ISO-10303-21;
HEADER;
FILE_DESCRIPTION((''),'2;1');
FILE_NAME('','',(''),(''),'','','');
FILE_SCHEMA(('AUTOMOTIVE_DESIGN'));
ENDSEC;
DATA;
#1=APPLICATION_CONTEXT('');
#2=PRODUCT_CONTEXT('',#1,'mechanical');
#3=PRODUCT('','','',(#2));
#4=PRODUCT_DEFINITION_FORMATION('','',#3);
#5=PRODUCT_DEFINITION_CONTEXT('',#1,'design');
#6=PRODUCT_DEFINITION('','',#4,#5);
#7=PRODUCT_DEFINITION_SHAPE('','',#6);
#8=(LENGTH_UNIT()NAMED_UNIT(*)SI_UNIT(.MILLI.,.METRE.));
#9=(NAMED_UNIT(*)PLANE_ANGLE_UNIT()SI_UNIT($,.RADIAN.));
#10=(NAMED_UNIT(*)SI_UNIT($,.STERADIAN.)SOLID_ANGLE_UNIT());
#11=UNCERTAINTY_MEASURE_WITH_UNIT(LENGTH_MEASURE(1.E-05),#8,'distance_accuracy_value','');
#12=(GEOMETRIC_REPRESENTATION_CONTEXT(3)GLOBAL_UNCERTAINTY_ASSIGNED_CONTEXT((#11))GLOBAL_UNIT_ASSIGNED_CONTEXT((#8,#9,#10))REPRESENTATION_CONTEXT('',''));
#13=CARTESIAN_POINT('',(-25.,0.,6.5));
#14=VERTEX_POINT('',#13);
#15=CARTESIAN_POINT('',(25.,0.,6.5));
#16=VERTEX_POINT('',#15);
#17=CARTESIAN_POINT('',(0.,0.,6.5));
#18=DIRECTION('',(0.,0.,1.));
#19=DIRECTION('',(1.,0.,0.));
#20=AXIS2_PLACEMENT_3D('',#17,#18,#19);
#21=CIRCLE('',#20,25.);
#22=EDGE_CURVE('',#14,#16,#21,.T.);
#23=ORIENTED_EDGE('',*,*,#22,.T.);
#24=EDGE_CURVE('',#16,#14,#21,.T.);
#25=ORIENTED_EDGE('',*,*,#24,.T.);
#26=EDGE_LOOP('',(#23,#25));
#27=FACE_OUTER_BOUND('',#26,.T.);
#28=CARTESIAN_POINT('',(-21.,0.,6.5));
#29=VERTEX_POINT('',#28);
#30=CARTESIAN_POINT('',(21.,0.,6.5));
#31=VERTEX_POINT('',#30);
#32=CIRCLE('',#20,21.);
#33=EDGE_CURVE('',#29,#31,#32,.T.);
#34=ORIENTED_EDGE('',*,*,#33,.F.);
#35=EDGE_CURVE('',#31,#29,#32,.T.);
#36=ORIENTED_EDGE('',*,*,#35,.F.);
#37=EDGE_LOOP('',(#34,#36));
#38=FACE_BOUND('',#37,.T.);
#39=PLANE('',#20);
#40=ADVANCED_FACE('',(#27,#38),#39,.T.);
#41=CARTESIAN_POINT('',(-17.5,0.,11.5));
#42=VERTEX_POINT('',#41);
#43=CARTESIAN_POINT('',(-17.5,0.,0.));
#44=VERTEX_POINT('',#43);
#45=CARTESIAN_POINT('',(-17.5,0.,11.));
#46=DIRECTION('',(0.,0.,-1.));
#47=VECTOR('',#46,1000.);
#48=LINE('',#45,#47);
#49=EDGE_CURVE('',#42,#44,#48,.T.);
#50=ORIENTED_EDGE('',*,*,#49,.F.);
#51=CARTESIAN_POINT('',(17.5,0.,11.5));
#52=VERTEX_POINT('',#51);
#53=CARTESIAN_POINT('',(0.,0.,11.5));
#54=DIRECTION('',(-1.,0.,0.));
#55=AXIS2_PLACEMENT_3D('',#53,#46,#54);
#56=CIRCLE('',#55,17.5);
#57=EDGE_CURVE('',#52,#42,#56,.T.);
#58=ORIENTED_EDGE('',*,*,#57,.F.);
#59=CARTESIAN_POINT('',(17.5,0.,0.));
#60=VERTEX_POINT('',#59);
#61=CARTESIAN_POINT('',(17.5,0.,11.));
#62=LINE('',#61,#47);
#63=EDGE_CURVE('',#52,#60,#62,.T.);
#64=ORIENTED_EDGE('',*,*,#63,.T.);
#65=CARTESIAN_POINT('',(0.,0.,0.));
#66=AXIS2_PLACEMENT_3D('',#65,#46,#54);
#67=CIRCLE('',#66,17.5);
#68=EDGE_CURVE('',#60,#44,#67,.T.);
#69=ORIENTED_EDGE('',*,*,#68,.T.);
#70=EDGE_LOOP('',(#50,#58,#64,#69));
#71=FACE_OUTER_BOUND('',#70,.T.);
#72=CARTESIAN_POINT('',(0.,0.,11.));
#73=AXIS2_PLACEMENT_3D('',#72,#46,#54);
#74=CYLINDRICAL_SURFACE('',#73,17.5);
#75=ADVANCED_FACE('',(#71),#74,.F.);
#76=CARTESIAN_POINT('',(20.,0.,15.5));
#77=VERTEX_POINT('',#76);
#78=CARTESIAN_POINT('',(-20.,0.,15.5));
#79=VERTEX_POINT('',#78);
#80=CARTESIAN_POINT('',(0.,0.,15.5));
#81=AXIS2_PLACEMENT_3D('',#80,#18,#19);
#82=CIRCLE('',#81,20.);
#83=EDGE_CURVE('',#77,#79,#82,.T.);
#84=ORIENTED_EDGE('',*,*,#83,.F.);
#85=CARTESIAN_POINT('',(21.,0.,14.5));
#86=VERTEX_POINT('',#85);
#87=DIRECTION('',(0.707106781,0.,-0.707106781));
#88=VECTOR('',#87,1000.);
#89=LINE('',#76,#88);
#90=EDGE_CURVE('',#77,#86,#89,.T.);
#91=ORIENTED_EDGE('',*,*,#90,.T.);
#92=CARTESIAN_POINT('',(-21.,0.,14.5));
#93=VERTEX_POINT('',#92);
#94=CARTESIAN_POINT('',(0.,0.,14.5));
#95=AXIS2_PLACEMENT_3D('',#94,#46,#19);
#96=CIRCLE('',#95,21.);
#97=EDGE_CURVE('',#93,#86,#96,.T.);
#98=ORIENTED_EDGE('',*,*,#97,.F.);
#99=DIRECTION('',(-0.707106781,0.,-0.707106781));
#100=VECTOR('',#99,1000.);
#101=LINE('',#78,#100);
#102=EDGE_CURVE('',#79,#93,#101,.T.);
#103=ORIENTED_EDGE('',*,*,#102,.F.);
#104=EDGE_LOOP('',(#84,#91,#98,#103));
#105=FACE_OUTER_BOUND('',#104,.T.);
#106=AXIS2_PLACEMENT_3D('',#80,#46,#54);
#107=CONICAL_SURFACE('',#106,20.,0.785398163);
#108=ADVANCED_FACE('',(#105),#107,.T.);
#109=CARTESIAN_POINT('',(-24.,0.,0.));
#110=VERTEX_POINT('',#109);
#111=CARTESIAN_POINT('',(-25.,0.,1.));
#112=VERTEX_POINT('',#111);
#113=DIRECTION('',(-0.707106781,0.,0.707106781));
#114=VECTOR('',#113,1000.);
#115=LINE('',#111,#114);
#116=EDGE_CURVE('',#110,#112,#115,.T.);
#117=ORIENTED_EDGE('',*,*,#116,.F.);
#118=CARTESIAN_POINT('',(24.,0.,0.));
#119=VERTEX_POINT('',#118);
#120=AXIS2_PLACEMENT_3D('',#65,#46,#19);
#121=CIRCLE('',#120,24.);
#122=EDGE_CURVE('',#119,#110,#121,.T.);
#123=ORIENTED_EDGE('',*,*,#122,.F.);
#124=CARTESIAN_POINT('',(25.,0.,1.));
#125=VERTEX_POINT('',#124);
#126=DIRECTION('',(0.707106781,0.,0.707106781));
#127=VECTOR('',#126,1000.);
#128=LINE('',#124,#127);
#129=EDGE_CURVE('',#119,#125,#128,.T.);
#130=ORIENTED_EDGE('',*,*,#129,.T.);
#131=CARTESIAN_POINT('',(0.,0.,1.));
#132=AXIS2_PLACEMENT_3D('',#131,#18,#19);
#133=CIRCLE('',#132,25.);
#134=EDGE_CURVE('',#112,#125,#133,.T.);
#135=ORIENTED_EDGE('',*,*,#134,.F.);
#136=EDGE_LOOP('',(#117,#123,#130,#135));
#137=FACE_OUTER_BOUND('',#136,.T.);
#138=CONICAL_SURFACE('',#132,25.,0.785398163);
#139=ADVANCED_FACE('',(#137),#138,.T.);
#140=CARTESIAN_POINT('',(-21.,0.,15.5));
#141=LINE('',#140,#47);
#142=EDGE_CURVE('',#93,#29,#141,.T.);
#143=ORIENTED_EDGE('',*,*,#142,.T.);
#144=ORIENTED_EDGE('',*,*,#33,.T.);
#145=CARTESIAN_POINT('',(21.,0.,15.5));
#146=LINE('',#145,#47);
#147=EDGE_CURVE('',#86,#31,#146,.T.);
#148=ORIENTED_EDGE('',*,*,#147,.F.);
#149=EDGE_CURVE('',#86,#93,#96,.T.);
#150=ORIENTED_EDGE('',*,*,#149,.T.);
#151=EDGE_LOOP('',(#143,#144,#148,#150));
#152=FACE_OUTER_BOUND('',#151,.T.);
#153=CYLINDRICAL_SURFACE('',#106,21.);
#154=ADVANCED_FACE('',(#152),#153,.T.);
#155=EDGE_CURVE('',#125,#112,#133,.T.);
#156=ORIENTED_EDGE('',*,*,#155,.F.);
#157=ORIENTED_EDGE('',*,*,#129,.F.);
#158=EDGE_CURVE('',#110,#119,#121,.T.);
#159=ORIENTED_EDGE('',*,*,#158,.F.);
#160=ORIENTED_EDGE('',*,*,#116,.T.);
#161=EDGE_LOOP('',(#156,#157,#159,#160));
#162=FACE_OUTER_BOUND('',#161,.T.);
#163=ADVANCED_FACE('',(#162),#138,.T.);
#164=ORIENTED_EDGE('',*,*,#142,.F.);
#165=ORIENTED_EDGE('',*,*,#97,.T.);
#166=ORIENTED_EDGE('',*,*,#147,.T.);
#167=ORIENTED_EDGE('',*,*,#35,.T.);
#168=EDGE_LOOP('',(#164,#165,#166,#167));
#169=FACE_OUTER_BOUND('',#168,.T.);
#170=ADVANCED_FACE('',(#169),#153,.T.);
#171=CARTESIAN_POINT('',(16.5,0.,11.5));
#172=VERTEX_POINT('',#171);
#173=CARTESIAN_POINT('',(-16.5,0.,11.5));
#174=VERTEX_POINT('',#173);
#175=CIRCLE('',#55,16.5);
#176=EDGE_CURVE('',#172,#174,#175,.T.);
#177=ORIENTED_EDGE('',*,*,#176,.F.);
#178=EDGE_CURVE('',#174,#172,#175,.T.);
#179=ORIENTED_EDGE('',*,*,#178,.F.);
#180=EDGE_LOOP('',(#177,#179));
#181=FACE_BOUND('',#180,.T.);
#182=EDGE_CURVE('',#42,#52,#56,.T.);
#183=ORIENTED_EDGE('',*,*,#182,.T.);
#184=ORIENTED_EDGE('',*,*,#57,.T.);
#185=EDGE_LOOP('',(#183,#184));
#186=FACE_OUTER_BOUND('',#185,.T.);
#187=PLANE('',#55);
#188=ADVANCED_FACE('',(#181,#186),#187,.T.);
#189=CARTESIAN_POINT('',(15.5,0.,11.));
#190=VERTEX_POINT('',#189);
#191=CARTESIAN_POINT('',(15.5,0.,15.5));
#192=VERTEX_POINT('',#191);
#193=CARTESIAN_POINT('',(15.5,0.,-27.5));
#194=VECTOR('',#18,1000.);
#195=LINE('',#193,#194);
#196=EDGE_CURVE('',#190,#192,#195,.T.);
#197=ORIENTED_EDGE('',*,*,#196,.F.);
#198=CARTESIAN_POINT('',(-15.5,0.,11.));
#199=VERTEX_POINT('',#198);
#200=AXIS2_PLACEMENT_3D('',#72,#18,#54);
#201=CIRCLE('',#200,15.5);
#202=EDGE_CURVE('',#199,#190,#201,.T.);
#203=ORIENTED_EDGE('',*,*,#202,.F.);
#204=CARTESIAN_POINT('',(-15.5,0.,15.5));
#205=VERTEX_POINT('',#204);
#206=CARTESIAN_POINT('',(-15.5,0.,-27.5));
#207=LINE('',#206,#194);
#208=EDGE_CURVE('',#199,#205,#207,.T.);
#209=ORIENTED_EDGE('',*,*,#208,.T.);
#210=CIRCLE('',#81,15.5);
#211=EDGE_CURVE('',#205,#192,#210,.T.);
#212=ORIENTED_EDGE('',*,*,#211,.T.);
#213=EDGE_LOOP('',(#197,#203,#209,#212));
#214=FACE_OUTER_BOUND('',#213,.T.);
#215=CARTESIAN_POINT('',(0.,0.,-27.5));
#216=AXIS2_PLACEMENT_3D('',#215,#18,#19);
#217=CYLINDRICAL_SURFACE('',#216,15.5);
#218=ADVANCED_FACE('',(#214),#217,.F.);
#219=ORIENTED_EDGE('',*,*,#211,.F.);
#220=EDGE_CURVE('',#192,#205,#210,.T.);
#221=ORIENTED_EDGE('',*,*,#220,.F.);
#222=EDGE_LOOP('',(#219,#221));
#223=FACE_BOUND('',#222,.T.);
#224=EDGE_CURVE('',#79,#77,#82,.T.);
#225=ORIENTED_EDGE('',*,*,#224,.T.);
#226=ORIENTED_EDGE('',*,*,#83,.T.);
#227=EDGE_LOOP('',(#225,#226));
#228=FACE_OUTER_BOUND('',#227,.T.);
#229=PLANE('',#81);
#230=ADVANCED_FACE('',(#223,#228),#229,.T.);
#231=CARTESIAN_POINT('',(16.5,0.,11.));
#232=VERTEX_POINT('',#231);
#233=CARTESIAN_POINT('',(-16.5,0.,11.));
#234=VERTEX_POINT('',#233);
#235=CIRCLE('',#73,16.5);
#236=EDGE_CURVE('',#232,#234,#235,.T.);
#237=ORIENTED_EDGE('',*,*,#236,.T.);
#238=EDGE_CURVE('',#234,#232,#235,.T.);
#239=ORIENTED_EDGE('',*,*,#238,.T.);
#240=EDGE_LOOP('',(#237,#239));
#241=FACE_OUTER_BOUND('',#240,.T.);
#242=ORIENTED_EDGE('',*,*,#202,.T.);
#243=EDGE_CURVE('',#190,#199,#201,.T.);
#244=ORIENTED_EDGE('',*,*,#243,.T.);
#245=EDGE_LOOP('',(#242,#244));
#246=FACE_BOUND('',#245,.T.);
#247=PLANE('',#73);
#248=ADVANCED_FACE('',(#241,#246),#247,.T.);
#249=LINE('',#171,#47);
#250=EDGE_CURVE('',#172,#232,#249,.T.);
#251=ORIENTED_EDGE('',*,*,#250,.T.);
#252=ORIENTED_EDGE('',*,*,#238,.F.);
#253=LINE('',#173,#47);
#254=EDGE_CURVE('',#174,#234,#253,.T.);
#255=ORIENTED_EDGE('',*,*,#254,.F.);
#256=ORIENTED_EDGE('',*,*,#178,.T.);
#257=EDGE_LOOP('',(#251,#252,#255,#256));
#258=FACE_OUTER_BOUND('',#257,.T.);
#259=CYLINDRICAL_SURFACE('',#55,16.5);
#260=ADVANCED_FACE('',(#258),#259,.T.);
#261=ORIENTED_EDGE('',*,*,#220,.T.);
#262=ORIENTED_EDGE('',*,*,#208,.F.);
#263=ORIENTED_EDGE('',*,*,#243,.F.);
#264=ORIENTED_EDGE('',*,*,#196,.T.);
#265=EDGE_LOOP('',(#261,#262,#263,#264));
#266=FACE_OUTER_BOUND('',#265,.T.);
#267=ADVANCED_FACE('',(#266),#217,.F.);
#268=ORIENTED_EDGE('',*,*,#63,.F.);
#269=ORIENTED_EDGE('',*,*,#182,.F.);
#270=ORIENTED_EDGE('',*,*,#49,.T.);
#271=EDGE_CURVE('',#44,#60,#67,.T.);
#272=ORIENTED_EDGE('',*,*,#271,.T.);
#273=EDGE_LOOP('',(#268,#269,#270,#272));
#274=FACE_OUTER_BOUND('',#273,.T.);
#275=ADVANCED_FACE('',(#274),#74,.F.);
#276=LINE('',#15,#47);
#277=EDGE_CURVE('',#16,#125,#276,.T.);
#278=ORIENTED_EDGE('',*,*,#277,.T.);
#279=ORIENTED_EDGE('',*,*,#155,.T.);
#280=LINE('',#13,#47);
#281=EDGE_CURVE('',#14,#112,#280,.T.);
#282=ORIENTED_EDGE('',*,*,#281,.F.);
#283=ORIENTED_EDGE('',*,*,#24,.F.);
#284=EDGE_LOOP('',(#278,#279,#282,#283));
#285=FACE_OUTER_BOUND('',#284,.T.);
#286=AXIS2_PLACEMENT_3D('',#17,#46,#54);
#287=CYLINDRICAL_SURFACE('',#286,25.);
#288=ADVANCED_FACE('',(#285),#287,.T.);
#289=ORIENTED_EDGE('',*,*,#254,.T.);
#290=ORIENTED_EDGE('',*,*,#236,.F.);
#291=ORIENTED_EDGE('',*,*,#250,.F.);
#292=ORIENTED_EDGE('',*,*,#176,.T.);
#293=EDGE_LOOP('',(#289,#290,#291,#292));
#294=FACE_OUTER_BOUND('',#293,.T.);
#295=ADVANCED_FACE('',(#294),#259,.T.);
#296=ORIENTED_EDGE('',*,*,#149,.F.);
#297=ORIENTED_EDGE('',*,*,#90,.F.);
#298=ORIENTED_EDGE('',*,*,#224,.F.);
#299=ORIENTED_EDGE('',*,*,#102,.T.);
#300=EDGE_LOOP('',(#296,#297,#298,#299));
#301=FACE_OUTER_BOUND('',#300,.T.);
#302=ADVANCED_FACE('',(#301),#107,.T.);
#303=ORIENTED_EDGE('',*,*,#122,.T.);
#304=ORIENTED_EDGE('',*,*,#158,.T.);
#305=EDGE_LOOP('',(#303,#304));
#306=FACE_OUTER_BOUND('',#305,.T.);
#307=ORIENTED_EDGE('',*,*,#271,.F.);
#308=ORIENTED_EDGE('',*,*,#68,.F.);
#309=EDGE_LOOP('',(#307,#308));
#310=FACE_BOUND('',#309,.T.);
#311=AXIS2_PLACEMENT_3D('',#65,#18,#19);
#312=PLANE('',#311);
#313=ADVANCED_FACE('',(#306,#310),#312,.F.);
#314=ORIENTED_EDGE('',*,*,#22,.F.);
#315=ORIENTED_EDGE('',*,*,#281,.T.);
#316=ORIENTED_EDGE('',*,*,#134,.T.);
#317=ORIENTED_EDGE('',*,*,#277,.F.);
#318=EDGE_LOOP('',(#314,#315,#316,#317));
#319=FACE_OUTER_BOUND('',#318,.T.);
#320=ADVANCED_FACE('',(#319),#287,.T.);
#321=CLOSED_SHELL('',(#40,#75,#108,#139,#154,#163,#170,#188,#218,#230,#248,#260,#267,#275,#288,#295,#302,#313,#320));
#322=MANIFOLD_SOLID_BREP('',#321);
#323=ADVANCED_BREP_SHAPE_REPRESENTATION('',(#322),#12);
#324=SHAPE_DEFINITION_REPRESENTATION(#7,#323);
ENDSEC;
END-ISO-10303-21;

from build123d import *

# Parameters (mm, degrees)
SKETCH1_R           = 25
BOSS_EXTRUDE1_DEPTH = 6.5
SKETCH2_R           = 21
BOSS_EXTRUDE3_DEPTH = 9
SKETCH5_R           = 15.5
CUT_EXTRUDE2_DEPTH  = 43
SKETCH6_R           = 17.5
CUT_EXTRUDE3_DEPTH  = 11
SKETCH7_R           = 17.5
SKETCH7_R_2         = 16.5
CUT_EXTRUDE4_DEPTH  = 0.5
CHAMFER1_SIZE       = 1


with BuildPart() as part:
    # Sketch1 → Boss-Extrude1 (new body)
    with BuildSketch(Plane.XY):
        with Locations(Location((0, 0, 0), (0, 0, 180))):
            Circle(SKETCH1_R)
    extrude(amount=BOSS_EXTRUDE1_DEPTH)

    # Sketch2 → Boss-Extrude3 (add)
    with BuildSketch(Plane.XY.offset(6.5)):
        Circle(SKETCH2_R)
    extrude(amount=BOSS_EXTRUDE3_DEPTH)

    # Sketch5 → Cut-Extrude2 (cut)
    with BuildSketch(Plane.XY.offset(15.5)):
        Circle(SKETCH5_R)
    extrude(amount=-CUT_EXTRUDE2_DEPTH, mode=Mode.SUBTRACT)

    # Sketch6 → Cut-Extrude3 (cut)
    with BuildSketch(Plane(origin=(0, 0, 0), x_dir=(-1, 0, 0), z_dir=(0, 0, -1))):
        Circle(SKETCH6_R)
    extrude(amount=-CUT_EXTRUDE3_DEPTH, mode=Mode.SUBTRACT)

    # Sketch7 → Cut-Extrude4 (cut)
    with BuildSketch(Plane(origin=(0, 0, 11), x_dir=(-1, 0, 0), z_dir=(0, 0, -1))):
        Circle(SKETCH7_R)
        Circle(SKETCH7_R_2, mode=Mode.SUBTRACT)
    extrude(amount=-CUT_EXTRUDE4_DEPTH, mode=Mode.SUBTRACT)

    # Chamfer1
    chamfer1_edges = [part.edges().sort_by_distance(p)[0] for p in [
        (25, 0, 0),
        (-21, 0, 15.5),
    ]]
    chamfer(chamfer1_edges, length=CHAMFER1_SIZE)


solid = part.part
